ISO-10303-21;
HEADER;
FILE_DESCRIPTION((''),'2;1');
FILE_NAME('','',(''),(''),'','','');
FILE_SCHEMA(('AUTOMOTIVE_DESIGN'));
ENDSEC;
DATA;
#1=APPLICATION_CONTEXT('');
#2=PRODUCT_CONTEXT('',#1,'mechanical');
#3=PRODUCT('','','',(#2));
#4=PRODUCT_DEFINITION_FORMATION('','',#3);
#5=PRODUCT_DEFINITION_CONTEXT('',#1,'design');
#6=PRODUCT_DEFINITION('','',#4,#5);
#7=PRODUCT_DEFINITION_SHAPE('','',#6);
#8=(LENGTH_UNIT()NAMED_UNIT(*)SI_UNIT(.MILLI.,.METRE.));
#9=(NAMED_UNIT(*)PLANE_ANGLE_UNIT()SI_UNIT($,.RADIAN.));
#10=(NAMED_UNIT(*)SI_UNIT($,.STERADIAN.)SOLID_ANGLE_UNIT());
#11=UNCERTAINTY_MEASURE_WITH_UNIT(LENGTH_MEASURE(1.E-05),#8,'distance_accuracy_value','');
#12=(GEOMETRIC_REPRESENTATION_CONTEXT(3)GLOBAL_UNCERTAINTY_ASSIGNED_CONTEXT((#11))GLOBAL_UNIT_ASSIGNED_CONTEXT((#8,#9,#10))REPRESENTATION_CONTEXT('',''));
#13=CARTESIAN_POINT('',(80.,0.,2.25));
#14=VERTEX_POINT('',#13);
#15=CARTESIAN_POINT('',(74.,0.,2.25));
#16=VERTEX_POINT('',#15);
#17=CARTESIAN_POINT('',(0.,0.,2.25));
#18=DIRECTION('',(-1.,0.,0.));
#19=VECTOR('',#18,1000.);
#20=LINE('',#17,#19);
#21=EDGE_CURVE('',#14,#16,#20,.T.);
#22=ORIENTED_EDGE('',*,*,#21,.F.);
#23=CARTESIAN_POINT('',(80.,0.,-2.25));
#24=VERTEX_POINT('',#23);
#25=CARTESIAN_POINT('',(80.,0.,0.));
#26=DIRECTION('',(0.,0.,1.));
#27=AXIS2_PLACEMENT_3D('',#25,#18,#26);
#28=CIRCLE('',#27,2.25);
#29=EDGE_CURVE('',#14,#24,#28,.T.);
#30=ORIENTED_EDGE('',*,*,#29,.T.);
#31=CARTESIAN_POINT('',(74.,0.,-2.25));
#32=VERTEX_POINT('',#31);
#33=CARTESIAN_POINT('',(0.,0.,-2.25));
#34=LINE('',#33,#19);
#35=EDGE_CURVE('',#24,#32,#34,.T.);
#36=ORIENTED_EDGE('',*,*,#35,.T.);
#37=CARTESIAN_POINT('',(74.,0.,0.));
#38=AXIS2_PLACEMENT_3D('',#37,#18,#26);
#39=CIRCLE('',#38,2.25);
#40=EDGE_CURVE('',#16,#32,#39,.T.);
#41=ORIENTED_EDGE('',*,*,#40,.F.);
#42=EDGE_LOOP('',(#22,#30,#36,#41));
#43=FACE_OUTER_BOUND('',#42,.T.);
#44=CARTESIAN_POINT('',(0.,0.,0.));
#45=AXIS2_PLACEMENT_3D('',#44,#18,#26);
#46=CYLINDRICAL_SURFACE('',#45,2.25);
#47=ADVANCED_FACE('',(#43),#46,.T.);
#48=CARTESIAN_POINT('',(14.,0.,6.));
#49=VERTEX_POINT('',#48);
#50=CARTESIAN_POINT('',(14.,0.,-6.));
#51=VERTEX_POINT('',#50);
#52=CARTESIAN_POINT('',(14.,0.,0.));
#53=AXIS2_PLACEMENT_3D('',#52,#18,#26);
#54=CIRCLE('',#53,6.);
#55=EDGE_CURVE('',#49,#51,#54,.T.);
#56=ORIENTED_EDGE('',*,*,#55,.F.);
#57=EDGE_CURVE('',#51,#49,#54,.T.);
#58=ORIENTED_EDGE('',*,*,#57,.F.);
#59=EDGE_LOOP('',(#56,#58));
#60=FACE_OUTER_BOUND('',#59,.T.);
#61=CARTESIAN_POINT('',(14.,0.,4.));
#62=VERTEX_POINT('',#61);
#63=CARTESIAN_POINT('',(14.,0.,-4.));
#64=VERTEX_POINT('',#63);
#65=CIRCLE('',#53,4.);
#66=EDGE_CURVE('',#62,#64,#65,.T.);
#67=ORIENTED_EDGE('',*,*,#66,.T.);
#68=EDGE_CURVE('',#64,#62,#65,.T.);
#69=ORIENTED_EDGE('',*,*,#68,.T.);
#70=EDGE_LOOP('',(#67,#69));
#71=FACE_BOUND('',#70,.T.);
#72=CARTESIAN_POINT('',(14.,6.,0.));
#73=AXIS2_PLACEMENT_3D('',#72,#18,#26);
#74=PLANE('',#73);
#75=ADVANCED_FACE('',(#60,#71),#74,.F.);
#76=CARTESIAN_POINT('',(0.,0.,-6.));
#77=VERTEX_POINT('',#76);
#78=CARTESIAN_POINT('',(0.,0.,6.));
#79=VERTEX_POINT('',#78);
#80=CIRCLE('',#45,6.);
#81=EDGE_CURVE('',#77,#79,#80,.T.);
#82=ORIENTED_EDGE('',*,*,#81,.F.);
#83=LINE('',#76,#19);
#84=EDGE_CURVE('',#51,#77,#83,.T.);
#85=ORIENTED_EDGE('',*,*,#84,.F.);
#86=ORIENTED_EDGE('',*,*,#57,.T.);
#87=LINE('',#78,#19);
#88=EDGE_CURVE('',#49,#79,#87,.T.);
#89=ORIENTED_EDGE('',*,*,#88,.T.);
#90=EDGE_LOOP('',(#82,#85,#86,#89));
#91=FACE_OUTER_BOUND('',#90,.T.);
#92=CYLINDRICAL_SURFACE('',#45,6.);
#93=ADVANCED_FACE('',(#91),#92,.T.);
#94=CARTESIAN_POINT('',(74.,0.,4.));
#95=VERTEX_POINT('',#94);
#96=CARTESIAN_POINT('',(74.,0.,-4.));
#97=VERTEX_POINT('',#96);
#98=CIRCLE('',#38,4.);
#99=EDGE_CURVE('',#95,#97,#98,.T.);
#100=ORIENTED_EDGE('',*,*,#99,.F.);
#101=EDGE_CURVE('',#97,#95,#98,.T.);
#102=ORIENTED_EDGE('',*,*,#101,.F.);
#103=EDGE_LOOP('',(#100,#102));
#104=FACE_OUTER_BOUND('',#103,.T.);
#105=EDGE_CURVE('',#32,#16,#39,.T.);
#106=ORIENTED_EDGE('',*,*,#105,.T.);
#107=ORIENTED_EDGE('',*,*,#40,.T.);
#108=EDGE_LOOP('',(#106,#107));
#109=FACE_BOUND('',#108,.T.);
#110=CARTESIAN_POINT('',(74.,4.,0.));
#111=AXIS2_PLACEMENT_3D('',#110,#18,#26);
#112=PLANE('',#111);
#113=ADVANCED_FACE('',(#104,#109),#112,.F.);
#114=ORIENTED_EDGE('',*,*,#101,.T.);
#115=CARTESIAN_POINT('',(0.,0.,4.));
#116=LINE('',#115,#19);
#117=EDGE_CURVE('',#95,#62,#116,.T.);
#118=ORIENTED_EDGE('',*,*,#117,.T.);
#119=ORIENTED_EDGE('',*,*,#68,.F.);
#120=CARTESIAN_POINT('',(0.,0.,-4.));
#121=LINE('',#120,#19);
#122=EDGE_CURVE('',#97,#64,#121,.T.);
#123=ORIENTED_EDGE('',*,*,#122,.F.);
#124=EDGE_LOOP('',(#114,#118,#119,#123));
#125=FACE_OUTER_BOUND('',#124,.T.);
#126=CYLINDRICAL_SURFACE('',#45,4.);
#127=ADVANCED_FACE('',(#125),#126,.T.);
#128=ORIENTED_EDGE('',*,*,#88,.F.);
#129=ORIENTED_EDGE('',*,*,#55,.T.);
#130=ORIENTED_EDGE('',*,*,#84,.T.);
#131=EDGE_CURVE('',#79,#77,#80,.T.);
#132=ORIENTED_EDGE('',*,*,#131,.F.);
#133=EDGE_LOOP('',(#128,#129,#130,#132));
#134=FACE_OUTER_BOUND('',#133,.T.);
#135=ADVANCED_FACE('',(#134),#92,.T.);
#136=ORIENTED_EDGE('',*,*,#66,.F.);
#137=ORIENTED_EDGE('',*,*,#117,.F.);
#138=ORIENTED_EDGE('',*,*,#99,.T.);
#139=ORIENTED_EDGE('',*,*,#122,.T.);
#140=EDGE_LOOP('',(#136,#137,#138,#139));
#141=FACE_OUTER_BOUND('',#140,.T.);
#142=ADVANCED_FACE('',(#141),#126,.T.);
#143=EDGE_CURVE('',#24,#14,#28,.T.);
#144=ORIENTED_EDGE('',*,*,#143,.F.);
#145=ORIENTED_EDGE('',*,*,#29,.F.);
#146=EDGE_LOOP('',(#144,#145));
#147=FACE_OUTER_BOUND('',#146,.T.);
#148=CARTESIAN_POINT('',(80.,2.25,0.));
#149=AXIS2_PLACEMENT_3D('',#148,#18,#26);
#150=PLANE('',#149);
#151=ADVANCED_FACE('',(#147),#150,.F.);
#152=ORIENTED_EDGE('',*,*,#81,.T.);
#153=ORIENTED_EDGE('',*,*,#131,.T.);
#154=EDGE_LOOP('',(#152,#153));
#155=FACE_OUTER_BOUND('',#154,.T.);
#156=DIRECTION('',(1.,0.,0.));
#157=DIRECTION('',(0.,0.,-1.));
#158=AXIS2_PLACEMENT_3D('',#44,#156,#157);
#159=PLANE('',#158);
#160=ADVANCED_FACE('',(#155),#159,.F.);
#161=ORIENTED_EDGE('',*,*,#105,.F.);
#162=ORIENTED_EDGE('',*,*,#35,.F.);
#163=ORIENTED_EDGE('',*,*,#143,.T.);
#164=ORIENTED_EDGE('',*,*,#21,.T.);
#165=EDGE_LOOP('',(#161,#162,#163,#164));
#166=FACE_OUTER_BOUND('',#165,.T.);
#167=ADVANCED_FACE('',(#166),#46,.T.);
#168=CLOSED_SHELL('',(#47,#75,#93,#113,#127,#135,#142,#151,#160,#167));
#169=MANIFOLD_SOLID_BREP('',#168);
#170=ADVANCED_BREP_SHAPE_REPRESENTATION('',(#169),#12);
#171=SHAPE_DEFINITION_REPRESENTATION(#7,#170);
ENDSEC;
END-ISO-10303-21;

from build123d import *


with BuildPart() as part:
    # Stepped Shaft Profile → Stepped Shaft Revolve (revolve)
    with BuildSketch(Plane.XY, mode=Mode.PRIVATE) as stepped_shaft_revolve_sk:
        Polygon((0, 0), (0, 6), (14, 6), (14, 4), (74, 4), (74, 2.25), (80, 2.25), (80, 0), align=None)
    revolve(stepped_shaft_revolve_sk.sketch.rotate(Axis((0, 0, 0), (1, 0, 0)), 90), axis=Axis((0, 0, 0), (1, 0, 0)))


solid = part.part
